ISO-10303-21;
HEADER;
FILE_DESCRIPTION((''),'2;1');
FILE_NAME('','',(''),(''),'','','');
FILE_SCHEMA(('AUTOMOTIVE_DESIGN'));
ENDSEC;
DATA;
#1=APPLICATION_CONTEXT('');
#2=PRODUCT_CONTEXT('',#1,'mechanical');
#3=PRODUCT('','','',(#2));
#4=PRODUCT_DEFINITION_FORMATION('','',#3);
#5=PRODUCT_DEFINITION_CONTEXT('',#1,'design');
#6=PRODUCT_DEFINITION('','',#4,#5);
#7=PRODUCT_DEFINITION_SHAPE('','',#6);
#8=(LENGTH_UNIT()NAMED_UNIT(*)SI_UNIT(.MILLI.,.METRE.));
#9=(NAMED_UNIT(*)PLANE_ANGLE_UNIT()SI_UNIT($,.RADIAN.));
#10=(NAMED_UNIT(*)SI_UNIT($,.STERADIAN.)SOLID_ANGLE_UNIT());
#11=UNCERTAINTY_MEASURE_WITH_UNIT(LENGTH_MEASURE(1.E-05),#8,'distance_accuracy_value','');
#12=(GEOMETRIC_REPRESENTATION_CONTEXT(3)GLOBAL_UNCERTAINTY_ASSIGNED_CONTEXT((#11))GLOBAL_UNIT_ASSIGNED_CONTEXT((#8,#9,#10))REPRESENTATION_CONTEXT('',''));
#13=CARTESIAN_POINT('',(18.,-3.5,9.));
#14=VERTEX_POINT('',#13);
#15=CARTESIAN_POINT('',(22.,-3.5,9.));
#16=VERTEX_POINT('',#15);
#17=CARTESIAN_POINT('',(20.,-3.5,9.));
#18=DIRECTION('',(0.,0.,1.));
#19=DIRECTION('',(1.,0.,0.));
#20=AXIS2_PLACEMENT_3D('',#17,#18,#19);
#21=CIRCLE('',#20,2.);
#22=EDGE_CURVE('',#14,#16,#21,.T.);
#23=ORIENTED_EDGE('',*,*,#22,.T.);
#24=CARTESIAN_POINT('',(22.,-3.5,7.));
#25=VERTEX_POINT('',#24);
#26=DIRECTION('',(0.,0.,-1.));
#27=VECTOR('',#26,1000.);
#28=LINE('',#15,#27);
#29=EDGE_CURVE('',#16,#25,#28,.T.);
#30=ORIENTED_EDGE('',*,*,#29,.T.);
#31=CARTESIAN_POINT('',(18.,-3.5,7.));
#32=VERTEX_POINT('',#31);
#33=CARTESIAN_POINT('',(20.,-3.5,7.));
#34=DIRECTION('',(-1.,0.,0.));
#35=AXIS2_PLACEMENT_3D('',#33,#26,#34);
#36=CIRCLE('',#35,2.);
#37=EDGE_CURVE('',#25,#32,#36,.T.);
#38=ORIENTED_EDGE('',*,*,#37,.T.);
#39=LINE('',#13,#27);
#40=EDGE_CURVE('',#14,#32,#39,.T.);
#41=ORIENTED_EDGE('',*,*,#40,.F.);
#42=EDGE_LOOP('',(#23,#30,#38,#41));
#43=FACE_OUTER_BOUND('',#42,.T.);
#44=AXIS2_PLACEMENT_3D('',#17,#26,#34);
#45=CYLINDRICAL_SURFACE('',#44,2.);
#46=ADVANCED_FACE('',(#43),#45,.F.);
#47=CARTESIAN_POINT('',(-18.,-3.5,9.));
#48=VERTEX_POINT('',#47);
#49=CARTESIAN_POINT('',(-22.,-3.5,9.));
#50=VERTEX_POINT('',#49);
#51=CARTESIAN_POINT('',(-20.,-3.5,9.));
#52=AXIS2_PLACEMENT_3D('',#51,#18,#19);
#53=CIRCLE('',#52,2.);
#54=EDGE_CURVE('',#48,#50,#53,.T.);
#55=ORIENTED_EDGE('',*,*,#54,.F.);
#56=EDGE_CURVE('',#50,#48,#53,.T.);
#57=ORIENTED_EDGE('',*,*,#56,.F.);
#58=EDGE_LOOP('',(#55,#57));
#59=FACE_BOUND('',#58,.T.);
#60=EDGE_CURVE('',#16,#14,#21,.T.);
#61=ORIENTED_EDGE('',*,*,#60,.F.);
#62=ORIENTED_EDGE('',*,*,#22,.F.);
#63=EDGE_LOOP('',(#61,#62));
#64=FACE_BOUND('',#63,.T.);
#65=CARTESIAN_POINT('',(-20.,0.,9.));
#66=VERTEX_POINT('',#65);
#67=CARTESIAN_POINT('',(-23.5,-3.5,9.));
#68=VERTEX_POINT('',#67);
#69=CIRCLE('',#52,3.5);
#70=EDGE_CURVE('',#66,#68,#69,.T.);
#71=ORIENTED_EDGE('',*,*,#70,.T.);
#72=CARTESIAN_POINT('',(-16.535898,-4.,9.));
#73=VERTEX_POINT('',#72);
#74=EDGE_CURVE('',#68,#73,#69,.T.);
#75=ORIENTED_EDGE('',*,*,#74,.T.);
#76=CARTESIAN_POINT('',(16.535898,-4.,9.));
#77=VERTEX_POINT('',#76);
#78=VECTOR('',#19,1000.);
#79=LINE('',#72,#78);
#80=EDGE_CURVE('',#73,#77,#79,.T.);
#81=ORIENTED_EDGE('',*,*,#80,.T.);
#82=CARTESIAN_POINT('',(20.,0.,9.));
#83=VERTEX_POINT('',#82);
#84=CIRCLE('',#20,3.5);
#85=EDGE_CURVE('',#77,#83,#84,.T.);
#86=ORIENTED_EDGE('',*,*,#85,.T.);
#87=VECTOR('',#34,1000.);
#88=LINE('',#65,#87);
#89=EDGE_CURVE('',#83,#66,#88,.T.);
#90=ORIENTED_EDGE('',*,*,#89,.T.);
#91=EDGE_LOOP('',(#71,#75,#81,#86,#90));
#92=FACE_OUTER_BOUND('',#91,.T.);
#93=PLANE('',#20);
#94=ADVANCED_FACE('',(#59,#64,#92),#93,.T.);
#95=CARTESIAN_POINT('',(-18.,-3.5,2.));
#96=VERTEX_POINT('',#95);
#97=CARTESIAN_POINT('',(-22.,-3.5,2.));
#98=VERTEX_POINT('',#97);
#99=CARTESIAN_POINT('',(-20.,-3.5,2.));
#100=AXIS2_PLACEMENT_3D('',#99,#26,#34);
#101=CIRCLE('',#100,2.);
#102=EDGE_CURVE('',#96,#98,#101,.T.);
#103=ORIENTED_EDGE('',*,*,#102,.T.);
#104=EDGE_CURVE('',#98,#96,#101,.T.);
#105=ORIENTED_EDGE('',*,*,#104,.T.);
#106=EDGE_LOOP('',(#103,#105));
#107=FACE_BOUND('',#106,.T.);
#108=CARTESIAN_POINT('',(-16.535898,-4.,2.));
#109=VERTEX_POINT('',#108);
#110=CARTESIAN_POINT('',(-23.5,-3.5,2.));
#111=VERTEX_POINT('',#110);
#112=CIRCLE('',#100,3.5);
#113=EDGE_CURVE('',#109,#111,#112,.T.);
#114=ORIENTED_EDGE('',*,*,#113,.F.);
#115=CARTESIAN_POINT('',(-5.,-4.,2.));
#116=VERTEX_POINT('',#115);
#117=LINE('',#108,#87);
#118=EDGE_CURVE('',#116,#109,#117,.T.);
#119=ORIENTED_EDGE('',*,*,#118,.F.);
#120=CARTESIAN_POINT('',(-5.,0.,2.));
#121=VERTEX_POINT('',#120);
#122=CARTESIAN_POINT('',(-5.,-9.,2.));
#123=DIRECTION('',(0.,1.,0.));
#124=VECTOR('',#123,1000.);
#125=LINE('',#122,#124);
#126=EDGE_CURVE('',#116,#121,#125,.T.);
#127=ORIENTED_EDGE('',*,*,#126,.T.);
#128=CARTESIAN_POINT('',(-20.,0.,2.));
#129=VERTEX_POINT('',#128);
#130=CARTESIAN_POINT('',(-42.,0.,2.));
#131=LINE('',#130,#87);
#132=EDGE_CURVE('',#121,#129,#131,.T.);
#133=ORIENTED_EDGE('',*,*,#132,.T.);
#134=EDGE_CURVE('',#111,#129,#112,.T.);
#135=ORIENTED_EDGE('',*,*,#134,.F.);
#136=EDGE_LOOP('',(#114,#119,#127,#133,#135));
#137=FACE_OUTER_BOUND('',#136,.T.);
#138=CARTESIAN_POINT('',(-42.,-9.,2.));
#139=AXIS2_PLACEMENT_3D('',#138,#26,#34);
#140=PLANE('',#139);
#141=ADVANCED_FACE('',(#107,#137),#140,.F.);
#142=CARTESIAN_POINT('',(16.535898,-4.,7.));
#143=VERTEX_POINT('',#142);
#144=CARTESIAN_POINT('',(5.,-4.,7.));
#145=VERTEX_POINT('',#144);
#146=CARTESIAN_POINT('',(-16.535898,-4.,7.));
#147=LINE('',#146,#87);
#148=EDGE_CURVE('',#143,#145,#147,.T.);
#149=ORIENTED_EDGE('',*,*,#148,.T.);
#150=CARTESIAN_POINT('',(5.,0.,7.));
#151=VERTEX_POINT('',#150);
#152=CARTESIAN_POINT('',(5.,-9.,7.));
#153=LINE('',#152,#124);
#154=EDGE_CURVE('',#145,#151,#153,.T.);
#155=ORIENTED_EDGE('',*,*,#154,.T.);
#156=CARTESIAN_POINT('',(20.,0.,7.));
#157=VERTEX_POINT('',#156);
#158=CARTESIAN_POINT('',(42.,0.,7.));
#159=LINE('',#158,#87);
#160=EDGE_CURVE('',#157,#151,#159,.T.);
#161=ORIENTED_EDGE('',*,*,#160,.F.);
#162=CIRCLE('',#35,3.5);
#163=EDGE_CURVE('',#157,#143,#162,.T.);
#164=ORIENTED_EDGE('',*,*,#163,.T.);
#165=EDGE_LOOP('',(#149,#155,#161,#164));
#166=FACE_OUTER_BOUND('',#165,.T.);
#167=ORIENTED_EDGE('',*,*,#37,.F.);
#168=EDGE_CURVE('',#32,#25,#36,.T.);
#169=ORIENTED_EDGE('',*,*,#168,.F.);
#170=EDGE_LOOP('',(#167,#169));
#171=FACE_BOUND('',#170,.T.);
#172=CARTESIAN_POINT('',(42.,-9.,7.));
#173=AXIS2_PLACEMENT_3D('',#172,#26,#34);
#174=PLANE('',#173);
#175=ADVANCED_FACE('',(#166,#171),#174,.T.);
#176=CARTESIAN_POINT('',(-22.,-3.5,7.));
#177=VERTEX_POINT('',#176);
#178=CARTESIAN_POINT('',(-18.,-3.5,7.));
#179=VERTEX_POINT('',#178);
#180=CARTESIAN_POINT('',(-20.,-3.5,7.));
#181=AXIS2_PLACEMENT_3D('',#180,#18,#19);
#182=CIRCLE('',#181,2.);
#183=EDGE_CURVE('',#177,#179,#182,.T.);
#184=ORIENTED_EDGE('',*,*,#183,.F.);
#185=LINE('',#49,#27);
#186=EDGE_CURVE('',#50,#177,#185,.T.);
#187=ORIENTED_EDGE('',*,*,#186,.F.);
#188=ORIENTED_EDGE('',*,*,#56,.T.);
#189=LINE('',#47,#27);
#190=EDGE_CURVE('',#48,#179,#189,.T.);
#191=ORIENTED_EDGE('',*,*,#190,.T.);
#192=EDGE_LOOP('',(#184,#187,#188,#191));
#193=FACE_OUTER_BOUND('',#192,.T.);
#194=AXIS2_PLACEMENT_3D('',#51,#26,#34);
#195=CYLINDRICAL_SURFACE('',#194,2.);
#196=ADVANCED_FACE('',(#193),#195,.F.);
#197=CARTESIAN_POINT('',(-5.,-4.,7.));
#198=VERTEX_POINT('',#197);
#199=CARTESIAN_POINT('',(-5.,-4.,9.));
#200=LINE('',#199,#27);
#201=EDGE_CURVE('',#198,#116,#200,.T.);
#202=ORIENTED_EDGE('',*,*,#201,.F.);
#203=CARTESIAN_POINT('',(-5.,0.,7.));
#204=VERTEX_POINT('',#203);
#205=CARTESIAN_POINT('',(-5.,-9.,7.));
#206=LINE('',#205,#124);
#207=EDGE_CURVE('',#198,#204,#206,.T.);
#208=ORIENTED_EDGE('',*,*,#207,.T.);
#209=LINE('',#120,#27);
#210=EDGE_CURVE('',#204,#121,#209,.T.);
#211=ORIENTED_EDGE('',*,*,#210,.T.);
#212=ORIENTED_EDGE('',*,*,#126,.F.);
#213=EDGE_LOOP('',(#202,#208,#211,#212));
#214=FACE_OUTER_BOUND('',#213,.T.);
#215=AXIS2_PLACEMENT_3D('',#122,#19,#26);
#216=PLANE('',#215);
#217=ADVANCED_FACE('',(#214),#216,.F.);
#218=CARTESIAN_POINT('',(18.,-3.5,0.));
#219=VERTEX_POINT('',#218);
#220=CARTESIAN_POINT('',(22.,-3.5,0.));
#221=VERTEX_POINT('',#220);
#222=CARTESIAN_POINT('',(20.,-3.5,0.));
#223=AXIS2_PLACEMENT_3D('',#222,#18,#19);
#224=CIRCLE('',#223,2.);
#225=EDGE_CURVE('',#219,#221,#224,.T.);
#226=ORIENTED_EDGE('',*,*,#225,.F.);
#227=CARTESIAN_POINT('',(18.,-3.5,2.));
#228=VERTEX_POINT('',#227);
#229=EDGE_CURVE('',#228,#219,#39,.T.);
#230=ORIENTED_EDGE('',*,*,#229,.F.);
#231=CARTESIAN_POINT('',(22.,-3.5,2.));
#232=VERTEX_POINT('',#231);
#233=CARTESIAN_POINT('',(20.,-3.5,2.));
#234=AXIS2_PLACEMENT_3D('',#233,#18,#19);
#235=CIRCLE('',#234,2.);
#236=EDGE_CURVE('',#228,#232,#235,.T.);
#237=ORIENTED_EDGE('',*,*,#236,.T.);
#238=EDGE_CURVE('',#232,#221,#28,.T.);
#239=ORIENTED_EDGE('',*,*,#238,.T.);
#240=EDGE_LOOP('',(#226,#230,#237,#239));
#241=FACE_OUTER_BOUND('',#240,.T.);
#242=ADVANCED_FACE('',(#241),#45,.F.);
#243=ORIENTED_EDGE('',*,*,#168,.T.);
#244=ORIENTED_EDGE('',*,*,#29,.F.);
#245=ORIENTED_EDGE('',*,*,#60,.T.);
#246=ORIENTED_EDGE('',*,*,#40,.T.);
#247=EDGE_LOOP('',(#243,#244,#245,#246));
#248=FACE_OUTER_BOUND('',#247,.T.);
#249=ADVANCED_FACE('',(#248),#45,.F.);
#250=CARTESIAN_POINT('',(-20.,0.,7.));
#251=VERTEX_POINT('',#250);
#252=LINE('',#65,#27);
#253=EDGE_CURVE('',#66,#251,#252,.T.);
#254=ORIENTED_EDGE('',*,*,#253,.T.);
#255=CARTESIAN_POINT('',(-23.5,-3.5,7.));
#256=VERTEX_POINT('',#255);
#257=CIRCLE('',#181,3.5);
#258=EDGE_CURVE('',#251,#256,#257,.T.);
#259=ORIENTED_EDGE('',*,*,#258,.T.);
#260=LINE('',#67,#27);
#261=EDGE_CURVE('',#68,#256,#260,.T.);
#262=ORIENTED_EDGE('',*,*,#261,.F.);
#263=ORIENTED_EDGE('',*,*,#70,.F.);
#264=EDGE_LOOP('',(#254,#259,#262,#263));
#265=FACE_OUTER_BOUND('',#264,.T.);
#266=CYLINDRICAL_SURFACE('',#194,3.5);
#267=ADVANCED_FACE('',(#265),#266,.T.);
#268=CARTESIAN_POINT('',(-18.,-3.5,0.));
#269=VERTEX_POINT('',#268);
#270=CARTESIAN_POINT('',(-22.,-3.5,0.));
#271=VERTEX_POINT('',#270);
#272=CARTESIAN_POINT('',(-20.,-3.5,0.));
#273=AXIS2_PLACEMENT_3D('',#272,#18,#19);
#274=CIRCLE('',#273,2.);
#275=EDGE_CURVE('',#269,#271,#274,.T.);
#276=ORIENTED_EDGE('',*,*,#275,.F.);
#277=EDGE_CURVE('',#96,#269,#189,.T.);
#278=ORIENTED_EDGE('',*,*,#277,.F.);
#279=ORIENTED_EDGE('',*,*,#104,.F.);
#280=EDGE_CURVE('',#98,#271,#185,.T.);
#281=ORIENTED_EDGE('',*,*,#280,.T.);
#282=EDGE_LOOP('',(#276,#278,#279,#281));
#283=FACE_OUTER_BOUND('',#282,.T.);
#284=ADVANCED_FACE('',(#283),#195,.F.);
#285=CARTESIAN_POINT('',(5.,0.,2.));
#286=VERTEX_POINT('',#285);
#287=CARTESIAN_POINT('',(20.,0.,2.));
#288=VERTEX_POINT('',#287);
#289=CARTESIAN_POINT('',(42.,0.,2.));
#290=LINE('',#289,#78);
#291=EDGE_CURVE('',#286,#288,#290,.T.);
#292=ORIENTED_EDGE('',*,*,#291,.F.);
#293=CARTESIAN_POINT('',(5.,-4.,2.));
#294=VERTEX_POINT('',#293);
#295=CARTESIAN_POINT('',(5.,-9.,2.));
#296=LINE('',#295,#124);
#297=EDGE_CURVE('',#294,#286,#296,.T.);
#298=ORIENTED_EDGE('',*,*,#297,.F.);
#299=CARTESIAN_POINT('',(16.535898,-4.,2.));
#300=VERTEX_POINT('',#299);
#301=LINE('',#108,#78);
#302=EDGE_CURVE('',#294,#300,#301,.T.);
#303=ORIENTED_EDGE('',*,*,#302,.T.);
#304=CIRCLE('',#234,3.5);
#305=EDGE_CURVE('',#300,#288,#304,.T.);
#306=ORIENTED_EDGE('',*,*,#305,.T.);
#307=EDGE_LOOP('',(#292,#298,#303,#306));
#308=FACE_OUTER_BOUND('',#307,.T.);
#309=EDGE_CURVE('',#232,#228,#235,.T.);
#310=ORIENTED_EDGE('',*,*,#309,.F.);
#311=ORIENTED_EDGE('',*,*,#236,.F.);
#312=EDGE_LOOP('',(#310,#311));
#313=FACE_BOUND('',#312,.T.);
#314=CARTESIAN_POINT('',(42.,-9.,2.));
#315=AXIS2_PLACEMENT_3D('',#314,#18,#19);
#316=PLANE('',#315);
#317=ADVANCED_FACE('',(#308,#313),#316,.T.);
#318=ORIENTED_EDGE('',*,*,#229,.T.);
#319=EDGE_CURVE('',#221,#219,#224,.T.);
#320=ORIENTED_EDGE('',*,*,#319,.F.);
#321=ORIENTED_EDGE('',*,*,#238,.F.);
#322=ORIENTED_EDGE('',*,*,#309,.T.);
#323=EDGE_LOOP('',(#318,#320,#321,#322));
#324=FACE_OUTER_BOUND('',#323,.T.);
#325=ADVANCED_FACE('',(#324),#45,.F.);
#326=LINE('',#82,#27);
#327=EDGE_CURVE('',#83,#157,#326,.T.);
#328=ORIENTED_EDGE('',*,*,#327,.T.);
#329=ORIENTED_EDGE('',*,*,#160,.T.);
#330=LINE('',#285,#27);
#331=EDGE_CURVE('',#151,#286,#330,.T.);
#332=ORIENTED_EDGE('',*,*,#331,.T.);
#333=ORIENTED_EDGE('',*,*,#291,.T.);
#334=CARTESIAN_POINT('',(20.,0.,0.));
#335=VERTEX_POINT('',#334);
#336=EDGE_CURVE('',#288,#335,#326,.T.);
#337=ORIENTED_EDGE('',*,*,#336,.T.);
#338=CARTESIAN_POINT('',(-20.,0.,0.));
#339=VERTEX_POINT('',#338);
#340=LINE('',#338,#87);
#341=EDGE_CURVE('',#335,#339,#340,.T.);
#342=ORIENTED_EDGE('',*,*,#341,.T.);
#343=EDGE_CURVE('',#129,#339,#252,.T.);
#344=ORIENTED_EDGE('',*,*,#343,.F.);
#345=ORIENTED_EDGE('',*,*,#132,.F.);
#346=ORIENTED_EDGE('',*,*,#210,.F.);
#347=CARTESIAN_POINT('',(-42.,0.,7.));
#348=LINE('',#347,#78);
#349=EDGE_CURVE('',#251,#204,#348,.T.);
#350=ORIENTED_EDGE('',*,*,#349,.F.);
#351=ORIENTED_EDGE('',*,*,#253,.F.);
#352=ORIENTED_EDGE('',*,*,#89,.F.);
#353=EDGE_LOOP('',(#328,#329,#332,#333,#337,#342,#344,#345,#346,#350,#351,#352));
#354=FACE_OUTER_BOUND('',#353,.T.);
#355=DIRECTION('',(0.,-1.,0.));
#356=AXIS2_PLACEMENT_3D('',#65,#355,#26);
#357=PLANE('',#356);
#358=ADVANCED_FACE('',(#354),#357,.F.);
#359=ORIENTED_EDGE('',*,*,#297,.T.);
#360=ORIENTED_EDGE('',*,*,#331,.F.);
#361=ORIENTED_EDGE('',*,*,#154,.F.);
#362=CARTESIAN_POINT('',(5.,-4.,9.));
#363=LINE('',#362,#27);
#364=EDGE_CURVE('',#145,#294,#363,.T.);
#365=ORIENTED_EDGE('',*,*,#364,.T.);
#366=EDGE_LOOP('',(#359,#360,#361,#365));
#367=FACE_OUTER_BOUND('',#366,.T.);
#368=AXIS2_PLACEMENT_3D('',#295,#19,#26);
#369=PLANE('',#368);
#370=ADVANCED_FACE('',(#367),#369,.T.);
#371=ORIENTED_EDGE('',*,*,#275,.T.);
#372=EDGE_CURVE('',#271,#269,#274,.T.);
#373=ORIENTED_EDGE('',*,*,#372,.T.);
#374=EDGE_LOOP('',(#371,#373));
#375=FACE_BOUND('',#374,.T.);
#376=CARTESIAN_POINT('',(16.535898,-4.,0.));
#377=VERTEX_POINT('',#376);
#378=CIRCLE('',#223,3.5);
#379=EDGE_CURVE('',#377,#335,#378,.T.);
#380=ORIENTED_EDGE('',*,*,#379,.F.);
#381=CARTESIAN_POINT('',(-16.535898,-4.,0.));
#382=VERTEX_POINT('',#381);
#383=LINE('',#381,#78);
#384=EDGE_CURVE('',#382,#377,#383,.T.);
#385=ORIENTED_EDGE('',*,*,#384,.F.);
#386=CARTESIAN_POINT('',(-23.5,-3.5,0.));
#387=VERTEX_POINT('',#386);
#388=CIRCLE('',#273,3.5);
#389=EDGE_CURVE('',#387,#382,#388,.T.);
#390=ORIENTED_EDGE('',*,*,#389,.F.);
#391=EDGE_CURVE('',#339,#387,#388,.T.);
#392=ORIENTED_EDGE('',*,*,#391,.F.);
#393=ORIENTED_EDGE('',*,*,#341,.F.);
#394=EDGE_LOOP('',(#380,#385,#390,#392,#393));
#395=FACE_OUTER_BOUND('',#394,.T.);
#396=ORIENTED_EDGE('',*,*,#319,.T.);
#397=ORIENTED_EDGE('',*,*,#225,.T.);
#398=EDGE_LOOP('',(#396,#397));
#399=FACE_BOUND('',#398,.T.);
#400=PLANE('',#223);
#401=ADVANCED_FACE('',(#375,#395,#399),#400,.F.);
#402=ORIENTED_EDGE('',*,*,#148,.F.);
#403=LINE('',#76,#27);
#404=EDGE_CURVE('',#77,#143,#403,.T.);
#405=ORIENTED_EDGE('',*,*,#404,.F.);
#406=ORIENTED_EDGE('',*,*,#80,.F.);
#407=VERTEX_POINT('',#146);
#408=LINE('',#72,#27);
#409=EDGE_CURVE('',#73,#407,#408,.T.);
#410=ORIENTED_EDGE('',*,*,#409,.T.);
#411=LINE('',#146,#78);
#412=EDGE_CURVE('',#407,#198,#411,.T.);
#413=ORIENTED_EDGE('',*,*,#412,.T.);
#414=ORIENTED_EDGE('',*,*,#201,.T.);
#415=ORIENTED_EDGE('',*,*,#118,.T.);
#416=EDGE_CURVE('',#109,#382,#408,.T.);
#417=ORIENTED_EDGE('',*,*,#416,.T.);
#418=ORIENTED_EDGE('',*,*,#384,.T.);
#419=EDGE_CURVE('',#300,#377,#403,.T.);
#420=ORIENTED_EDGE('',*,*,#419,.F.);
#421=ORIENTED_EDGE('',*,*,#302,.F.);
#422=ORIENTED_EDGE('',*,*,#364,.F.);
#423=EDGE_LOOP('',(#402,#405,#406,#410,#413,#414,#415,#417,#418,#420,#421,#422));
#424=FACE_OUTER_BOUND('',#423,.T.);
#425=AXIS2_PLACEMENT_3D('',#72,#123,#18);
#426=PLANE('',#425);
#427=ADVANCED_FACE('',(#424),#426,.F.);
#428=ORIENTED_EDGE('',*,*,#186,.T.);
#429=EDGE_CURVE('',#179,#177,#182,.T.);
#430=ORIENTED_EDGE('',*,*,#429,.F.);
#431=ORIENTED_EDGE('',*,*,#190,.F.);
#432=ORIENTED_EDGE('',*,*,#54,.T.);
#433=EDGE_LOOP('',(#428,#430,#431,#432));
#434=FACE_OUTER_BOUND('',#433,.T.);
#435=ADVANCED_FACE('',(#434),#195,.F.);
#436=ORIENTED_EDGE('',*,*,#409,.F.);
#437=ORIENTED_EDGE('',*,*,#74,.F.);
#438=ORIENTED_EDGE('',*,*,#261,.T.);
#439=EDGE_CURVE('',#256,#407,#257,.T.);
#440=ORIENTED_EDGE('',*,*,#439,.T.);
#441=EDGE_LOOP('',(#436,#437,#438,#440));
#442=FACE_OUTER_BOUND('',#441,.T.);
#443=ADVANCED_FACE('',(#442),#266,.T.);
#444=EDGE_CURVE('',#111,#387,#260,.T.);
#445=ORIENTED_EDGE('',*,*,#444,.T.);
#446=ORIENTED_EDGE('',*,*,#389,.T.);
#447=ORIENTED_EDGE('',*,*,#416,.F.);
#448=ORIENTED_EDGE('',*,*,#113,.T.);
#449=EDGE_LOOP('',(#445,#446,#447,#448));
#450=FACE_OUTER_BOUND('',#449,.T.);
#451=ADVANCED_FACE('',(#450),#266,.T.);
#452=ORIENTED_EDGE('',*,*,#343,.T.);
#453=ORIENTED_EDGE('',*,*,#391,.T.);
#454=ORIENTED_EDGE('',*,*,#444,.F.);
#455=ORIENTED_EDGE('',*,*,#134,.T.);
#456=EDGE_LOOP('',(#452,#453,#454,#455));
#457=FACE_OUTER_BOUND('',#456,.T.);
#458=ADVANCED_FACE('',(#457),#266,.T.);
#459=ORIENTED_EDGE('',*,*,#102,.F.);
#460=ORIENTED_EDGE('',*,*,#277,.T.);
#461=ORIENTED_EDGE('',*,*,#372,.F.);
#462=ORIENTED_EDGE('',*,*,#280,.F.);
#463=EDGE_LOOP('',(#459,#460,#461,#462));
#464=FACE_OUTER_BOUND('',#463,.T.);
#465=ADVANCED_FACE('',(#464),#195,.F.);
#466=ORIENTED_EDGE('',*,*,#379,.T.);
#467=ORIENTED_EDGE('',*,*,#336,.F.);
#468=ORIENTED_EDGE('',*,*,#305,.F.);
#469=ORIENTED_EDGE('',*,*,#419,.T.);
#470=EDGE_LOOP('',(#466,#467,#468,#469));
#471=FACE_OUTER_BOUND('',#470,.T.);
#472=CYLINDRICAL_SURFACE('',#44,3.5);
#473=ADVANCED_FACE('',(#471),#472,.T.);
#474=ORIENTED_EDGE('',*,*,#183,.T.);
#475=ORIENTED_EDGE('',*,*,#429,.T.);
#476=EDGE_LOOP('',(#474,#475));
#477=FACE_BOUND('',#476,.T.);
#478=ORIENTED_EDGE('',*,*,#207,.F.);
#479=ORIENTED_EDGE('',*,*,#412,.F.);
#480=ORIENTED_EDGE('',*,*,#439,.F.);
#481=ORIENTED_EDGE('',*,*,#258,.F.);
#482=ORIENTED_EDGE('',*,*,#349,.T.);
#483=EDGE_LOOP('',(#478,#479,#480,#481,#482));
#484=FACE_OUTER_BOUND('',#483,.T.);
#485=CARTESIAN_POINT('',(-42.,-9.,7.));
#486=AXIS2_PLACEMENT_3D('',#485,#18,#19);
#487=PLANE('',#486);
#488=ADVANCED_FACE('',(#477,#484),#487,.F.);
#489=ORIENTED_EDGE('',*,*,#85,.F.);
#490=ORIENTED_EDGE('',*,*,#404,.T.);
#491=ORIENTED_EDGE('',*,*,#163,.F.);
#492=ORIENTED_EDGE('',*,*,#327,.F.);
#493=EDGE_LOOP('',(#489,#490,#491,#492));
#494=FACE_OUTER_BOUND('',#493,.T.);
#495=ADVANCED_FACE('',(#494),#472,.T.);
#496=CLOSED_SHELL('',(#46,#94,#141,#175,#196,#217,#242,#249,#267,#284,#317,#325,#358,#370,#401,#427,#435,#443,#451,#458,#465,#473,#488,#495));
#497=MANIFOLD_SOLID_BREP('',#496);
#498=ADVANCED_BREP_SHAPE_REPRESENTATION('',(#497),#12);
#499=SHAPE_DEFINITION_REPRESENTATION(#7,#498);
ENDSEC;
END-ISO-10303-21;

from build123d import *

# Parameters (mm, degrees)
SKETCH1_R           = 2
BOSS_EXTRUDE1_DEPTH = 9
SKETCH2_W           = 37
SKETCH2_H           = 5
CUT_EXTRUDE1_DEPTH  = 9


with BuildPart() as part:
    # Sketch1 → Boss-Extrude1 (new body)
    with BuildSketch(Plane.XY):
        with BuildLine():
            Line((-20, 0), (20, 0))
            ThreePointArc((20, 0), (22.645751311, -5.791287847), (16.535898385, -4))
            Line((16.535898385, -4), (-16.535898385, -4))
            ThreePointArc((-16.535898385, -4), (-22.645751311, -5.791287847), (-20, 0))
        make_face()
        with Locations((20, -3.5)):
            Circle(SKETCH1_R, mode=Mode.SUBTRACT)
        with Locations((-20, -3.5)):
            Circle(SKETCH1_R, mode=Mode.SUBTRACT)
    extrude(amount=BOSS_EXTRUDE1_DEPTH)

    # Sketch2 → Cut-Extrude1 (cut)
    with BuildSketch(Plane(origin=(0, 0, 0), x_dir=(1, 0, 0), z_dir=(0, 1, 0))):
        with Locations((-23.5, -4.5)):
            Rectangle(SKETCH2_W, SKETCH2_H)
    cut_extrude1 = extrude(amount=-CUT_EXTRUDE1_DEPTH, mode=Mode.SUBTRACT)

    # Mirror1: Cut-Extrude1 across plane
    add(cut_extrude1.mirror(Plane(origin=(0, 0, 0), x_dir=(0, 0, 1), z_dir=(1, 0, 0))), mode=Mode.SUBTRACT)


solid = part.part
